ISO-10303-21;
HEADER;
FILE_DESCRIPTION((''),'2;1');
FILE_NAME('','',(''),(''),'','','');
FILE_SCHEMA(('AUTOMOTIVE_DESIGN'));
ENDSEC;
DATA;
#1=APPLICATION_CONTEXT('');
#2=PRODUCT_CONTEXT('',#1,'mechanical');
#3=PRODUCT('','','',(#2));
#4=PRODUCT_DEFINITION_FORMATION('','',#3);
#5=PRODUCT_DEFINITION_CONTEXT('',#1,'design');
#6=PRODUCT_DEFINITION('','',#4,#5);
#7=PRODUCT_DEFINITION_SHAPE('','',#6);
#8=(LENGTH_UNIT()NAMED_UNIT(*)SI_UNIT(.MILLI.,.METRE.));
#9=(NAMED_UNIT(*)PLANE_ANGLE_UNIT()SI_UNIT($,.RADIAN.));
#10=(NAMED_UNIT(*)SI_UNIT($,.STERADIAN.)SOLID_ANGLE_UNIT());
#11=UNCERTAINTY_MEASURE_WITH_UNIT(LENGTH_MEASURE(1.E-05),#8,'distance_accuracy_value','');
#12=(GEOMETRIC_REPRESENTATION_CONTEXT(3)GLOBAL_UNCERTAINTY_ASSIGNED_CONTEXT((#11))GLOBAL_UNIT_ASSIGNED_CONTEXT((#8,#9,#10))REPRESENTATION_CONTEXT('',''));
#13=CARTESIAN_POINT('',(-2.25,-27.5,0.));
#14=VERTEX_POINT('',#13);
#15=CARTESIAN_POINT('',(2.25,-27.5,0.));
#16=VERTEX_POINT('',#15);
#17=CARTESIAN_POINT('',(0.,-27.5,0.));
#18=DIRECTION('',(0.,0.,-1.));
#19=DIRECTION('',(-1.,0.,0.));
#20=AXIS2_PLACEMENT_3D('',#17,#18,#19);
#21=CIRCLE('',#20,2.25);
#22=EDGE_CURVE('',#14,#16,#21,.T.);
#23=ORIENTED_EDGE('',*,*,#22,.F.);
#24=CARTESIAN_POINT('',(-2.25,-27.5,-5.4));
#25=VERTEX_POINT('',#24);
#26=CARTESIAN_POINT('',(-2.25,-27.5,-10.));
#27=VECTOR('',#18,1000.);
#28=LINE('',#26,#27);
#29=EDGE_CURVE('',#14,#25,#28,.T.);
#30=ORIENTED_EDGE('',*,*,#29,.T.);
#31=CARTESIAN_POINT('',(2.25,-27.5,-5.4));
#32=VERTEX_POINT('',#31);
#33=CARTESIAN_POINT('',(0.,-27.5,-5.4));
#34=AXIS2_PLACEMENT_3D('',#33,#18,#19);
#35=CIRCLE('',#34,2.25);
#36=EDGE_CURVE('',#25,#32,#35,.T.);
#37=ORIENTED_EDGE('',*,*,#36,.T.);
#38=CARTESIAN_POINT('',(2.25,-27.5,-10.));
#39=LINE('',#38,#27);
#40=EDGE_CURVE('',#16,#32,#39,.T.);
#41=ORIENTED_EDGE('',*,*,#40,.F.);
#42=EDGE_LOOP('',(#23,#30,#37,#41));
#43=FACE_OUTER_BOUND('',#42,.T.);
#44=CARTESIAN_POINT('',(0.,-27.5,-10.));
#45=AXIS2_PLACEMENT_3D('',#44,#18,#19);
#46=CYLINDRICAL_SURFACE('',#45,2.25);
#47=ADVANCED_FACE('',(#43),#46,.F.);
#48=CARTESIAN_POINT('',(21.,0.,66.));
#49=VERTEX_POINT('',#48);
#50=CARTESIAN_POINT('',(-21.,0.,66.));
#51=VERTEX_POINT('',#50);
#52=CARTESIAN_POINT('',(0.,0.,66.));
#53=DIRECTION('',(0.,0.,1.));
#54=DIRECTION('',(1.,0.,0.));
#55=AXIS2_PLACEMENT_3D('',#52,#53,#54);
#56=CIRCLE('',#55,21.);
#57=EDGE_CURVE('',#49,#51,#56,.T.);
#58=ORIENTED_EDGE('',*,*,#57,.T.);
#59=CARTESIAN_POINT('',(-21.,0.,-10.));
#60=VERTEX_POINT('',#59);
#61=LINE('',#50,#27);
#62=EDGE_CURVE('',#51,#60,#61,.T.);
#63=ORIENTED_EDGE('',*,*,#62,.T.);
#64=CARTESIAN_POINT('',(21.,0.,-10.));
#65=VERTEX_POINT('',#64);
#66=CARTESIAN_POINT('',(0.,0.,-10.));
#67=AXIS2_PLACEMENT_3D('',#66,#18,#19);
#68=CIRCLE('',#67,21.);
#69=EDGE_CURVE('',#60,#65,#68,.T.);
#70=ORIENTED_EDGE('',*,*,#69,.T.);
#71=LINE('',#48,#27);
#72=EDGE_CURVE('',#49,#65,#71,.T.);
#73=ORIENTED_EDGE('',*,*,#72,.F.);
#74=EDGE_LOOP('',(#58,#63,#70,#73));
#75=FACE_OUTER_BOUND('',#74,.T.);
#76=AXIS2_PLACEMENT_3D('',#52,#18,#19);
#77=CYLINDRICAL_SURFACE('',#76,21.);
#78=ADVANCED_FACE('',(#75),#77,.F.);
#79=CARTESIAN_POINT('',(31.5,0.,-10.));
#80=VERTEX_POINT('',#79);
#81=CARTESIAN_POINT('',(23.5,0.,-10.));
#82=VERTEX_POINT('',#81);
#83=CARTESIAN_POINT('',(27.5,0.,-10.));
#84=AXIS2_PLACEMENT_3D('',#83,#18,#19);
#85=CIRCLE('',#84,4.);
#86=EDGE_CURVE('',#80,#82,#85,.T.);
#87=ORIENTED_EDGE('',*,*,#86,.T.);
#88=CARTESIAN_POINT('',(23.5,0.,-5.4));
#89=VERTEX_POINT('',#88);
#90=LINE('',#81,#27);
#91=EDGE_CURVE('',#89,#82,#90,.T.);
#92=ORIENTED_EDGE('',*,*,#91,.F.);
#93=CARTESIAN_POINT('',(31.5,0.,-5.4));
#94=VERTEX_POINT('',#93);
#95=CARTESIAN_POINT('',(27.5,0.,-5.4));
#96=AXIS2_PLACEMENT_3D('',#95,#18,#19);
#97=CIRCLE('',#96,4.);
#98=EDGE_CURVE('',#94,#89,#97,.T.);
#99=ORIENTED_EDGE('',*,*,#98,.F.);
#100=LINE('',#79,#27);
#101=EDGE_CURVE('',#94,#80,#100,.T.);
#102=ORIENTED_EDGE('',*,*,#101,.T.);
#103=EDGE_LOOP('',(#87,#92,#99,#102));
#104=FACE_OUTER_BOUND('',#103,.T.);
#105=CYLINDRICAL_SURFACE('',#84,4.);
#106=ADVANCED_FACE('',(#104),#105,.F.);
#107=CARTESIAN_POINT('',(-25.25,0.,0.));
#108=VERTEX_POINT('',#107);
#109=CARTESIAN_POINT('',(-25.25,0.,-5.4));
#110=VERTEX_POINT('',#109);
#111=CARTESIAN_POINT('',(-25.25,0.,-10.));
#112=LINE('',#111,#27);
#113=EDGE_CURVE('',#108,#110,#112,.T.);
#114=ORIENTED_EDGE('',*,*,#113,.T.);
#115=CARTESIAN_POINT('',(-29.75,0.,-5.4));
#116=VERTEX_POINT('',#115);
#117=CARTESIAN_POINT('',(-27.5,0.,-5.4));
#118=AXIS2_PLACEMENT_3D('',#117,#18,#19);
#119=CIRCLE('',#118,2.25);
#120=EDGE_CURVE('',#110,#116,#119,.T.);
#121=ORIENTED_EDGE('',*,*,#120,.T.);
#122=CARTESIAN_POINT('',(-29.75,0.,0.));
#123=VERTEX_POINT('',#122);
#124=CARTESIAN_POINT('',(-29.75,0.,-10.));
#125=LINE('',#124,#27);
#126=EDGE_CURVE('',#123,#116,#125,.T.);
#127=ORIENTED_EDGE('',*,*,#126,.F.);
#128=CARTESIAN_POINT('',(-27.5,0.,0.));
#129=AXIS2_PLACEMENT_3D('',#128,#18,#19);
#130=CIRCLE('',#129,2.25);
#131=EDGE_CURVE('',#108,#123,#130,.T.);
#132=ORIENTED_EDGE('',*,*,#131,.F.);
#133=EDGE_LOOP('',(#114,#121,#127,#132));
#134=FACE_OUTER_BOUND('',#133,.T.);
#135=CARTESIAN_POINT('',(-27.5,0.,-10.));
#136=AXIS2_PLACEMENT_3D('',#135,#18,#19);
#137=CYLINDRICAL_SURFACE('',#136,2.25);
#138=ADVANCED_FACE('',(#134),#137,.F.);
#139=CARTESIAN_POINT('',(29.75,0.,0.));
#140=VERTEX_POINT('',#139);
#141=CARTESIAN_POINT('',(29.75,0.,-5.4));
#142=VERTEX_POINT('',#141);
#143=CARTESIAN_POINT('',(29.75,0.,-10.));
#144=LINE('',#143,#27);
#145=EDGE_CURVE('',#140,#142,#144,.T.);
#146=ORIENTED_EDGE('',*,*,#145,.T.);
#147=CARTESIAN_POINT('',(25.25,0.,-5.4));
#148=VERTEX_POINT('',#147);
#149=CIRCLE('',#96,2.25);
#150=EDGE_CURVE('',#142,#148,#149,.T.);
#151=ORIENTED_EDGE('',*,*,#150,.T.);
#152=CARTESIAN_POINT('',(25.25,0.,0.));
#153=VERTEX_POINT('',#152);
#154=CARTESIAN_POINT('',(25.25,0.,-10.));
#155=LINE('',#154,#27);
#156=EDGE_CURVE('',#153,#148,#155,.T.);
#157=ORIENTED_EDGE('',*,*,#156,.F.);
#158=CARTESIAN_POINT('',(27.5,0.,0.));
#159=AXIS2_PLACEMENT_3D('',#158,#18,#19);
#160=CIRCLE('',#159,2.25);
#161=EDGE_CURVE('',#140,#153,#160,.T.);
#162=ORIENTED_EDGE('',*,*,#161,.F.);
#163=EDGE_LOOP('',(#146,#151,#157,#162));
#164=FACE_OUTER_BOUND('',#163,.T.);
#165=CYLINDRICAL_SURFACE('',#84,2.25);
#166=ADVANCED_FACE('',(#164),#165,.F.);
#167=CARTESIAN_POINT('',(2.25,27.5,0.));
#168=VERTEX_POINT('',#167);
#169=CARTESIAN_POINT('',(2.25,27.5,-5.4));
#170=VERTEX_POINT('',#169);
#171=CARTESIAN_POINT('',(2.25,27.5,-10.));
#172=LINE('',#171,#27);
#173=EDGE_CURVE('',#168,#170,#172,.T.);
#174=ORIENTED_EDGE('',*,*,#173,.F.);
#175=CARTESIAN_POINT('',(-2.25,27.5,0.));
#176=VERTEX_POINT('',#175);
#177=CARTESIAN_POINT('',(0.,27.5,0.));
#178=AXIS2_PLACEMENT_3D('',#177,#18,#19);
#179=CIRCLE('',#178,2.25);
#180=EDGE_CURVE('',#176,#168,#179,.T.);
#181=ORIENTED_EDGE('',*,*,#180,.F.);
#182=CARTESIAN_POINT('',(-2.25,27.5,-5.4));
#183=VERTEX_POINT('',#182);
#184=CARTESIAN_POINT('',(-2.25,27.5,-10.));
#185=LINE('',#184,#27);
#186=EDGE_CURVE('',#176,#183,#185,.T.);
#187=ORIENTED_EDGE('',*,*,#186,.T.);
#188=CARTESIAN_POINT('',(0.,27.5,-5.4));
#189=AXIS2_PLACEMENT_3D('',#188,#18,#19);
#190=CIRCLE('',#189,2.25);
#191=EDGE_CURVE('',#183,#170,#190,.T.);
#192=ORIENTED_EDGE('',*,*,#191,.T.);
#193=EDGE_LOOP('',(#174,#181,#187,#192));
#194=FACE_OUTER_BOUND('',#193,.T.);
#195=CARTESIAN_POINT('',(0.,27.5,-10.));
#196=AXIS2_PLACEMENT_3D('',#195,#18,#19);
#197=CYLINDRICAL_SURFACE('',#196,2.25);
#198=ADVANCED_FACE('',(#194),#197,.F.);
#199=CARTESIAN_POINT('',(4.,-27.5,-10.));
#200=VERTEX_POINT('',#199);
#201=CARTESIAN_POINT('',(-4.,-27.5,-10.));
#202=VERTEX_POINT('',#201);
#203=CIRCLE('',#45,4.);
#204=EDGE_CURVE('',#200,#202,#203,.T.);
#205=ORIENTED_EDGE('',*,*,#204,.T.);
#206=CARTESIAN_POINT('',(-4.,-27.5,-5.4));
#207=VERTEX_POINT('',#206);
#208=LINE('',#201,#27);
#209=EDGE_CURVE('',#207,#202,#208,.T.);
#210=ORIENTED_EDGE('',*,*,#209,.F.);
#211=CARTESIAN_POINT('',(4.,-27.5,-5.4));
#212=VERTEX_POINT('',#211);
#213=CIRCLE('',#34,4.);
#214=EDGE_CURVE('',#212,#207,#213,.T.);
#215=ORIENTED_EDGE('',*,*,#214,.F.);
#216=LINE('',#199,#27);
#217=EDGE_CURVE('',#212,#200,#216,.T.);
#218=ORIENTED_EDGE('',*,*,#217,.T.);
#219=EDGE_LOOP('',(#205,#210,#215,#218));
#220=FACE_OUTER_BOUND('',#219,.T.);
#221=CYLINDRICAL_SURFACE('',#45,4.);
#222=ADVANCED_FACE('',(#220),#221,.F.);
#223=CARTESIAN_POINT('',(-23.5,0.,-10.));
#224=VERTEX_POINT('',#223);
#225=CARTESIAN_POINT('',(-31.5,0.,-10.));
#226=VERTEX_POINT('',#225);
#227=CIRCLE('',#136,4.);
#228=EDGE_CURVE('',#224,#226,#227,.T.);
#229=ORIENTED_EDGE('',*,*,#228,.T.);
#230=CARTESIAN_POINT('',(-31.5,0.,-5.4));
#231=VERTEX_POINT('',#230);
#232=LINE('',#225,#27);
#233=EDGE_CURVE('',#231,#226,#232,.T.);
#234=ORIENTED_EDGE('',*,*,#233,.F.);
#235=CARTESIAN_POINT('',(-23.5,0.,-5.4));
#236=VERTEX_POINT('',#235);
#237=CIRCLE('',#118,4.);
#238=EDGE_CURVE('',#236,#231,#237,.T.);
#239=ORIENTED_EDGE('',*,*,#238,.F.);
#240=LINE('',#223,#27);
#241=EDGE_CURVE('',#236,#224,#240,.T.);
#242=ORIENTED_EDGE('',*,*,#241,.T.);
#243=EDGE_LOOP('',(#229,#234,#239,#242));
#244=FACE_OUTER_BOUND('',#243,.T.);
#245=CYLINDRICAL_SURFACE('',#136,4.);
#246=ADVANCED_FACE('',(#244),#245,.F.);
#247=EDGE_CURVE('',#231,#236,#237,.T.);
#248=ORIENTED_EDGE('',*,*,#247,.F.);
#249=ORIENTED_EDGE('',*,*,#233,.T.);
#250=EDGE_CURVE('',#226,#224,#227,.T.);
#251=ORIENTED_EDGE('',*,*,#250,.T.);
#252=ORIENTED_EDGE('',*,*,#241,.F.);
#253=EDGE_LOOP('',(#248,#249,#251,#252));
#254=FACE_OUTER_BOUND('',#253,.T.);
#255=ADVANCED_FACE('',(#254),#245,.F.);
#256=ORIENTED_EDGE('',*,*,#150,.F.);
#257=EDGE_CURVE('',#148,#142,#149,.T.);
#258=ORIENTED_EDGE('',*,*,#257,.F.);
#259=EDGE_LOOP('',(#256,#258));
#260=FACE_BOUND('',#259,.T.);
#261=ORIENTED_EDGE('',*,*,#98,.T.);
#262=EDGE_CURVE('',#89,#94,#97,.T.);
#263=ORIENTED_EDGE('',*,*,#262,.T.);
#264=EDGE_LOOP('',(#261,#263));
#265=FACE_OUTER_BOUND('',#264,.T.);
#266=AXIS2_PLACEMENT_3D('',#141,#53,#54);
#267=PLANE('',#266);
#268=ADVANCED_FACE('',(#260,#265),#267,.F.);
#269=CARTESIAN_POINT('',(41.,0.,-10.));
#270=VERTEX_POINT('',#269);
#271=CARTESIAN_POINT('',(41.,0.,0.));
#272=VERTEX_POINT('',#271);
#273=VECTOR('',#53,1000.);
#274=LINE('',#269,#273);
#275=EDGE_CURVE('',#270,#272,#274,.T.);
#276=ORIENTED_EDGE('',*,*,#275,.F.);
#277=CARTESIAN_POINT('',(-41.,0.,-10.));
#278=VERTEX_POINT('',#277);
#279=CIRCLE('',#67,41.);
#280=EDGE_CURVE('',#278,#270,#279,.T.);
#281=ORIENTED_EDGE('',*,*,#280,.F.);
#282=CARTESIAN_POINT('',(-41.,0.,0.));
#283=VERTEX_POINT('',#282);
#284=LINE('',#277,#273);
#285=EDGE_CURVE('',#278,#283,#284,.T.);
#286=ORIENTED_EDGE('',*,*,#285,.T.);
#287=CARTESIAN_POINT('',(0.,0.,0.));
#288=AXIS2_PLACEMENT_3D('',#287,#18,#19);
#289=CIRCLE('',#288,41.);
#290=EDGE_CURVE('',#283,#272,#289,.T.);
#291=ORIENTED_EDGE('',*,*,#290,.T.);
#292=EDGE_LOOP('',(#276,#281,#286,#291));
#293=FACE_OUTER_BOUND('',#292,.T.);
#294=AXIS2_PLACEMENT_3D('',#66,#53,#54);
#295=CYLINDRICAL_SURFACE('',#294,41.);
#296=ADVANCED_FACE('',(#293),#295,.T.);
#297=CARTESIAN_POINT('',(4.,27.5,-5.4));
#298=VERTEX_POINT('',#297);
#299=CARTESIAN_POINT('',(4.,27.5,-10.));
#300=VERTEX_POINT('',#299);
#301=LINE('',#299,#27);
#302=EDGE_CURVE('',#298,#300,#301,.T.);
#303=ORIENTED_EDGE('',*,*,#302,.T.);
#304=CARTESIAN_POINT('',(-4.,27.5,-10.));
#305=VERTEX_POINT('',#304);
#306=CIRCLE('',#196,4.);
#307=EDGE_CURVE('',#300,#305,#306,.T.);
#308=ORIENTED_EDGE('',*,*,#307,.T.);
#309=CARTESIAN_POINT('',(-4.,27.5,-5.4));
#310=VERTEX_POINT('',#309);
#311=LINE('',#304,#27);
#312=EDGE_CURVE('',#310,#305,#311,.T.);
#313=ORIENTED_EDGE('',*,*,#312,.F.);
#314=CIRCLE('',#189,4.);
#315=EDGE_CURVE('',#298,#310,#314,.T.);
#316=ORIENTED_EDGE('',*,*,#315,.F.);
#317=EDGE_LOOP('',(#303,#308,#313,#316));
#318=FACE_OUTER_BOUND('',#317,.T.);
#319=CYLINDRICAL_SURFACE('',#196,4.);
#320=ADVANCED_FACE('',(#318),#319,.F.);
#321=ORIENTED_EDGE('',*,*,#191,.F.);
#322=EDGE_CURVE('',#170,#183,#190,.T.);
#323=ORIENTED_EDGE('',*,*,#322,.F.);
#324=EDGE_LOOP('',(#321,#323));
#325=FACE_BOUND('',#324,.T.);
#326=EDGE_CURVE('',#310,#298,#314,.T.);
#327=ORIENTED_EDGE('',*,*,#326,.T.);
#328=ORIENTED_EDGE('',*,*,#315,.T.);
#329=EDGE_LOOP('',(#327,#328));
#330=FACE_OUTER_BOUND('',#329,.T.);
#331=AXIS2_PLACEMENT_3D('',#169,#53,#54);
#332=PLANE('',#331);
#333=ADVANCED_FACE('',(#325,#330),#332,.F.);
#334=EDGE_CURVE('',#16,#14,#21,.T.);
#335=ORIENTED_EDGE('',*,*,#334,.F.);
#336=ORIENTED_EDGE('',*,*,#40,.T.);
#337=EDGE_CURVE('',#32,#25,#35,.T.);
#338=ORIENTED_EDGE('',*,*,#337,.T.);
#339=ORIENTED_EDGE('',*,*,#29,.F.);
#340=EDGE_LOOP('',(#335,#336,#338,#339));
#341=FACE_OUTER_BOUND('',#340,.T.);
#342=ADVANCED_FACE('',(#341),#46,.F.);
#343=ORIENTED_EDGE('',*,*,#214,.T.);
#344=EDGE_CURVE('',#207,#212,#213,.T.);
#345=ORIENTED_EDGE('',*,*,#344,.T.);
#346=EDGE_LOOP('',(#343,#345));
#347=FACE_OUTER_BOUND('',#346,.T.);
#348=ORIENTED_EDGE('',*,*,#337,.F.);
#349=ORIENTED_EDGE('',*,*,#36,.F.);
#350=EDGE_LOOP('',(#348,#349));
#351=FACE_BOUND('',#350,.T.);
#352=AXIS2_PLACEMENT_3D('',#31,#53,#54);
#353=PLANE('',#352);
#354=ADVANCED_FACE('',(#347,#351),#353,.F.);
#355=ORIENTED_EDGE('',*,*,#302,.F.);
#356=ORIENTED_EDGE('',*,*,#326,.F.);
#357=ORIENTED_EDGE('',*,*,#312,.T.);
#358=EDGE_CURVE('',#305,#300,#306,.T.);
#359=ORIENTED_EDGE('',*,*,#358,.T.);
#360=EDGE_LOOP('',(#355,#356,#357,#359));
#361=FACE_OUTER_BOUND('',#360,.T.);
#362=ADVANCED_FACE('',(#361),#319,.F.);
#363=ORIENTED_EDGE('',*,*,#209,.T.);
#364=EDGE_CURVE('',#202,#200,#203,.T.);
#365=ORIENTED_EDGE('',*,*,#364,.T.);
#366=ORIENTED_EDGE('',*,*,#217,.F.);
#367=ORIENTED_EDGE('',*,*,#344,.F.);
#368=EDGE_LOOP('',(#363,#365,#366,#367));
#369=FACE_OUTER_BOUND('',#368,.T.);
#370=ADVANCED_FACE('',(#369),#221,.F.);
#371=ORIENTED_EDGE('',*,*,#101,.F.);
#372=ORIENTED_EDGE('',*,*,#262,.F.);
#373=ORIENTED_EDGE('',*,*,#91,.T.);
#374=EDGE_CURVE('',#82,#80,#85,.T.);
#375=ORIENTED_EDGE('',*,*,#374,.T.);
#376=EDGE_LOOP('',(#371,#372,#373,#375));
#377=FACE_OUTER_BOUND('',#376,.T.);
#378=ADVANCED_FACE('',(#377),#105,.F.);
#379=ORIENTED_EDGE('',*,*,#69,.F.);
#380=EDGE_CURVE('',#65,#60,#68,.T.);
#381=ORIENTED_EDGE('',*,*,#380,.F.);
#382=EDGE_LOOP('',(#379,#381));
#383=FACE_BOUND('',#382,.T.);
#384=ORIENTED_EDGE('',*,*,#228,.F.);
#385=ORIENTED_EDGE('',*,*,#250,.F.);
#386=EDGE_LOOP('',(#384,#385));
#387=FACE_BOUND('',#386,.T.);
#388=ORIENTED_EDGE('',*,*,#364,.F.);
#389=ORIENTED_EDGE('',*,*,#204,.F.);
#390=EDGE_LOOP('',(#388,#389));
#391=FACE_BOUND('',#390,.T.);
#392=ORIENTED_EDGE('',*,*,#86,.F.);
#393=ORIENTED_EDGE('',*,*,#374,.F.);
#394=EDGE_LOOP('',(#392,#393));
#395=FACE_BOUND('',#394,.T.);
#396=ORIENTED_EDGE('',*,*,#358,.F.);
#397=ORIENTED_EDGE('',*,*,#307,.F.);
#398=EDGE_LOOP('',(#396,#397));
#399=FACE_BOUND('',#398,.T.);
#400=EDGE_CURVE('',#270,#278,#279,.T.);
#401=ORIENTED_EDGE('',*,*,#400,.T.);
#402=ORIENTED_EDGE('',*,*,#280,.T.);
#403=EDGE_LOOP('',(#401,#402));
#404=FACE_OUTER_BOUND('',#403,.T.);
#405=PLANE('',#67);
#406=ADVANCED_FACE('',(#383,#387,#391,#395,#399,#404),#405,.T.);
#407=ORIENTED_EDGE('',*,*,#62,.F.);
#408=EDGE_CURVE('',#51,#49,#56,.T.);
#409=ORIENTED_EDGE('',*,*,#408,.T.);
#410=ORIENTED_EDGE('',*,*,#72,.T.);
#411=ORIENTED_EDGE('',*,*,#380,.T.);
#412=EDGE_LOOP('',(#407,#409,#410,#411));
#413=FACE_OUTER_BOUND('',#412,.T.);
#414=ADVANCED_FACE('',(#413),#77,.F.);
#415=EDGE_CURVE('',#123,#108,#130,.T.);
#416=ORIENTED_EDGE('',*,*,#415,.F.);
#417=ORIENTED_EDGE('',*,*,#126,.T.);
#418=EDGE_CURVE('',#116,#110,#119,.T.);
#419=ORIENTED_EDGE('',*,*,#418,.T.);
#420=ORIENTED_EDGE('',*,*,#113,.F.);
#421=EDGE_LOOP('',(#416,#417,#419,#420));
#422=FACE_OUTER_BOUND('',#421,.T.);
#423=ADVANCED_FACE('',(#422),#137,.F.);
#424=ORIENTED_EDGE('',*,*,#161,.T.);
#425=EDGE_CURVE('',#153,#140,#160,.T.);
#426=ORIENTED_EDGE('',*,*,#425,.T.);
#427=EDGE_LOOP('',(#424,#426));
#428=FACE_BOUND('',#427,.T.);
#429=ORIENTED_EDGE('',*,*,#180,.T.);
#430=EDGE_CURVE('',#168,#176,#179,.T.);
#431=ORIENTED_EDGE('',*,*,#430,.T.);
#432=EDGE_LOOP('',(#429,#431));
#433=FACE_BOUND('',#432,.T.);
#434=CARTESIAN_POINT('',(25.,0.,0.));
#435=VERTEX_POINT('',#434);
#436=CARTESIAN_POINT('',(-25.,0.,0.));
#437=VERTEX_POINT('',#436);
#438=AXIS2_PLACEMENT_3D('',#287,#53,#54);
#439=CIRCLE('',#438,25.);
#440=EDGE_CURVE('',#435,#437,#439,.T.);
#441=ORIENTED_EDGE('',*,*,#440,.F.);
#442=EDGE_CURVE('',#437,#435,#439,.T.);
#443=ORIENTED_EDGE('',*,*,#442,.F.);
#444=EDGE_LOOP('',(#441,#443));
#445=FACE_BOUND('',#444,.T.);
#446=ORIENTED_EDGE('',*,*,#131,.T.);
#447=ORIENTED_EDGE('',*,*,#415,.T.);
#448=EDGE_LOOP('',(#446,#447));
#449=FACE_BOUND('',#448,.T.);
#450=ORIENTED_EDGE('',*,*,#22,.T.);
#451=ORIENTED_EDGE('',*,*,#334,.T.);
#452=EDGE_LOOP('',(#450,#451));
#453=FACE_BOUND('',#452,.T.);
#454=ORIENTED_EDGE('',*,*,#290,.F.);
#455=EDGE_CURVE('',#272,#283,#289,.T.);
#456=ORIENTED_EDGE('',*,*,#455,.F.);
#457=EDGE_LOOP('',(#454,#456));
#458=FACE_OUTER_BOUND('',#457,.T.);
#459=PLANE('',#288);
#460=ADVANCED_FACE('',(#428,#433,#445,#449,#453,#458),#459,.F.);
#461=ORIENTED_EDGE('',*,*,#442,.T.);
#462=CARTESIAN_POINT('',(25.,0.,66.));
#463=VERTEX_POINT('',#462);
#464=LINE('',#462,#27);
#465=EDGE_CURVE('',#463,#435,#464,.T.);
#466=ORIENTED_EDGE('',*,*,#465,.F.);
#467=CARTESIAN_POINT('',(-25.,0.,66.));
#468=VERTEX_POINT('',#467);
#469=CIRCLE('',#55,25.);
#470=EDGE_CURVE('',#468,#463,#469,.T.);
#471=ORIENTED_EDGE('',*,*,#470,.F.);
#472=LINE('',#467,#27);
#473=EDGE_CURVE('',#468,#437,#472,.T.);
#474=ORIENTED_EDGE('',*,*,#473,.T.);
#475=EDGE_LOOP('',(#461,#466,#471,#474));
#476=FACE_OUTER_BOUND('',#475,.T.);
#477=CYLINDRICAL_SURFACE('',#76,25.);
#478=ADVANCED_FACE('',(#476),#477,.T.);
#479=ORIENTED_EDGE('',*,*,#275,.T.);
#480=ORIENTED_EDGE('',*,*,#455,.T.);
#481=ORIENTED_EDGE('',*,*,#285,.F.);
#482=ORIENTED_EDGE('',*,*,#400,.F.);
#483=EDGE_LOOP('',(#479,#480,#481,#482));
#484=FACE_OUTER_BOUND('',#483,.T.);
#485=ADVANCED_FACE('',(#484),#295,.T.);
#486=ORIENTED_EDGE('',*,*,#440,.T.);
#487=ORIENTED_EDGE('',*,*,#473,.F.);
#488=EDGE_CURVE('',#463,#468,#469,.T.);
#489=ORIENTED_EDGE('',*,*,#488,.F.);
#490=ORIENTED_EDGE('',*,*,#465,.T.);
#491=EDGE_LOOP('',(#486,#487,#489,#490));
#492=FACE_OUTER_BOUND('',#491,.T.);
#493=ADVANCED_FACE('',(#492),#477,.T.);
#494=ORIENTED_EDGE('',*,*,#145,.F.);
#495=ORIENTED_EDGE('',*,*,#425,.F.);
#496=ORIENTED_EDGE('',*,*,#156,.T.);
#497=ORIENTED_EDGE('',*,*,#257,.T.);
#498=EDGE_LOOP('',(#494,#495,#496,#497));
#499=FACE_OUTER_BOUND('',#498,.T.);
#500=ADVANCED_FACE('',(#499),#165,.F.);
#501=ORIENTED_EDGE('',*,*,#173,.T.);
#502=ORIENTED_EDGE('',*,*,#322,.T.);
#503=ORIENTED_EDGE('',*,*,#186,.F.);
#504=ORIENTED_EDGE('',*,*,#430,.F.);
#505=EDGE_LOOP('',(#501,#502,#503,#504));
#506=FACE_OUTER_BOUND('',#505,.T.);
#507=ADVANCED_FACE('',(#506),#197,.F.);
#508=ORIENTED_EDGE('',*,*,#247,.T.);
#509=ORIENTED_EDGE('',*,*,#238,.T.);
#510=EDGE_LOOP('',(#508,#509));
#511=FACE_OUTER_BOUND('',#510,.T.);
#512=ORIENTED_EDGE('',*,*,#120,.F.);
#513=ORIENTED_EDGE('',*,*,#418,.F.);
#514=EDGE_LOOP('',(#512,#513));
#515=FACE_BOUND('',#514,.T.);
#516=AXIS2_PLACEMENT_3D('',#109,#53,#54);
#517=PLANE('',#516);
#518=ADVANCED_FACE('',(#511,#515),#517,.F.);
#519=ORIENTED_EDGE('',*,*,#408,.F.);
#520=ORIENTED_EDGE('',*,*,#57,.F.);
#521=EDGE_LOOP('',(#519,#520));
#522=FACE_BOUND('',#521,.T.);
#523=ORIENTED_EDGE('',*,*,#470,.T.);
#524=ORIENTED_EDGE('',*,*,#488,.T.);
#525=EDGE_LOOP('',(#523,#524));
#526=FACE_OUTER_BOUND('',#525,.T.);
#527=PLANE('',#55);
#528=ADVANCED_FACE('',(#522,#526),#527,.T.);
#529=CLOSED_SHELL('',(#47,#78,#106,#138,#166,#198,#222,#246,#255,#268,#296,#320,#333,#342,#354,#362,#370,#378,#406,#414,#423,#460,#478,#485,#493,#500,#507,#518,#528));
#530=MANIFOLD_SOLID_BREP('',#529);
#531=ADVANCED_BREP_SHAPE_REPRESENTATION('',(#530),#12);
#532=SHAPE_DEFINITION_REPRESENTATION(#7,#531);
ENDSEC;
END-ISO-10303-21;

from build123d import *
from build123d.topology import SkipClean

# Parameters (mm, degrees)
SKETCH_1_R                = 25
SKETCH_1_R_2              = 21
EXTRUDE_1_DEPTH           = 66
EXTRUDE_START             = 10
SKETCH_2_R                = 41
SKETCH_2_R_2              = 21
EXTRUDE_2_DEPTH           = 10
HOLE_WIZARD_1_D           = 4.5
HOLE_WIZARD_1_CBORE_D     = 8
HOLE_WIZARD_1_CBORE_DEPTH = 4.6
PATTERN_CIRCULAR_1_COUNT  = 4


with BuildPart() as part:
    # 草图1 → 凸台-拉伸1 (new body)
    with BuildSketch(Plane.XY):
        Circle(SKETCH_1_R)
        Circle(SKETCH_1_R_2, mode=Mode.SUBTRACT)
    extrude(amount=EXTRUDE_1_DEPTH)

    # 草图2 → 凸台-拉伸2 (add)
    with SkipClean():  # the faces are left unmerged after this step: merging them gives an invalid solid
        with BuildSketch(Plane(origin=(0, 0, 0), x_dir=(-1, 0, 0), z_dir=(0, 0, -1)).offset(EXTRUDE_START)):
            Circle(SKETCH_2_R)
            Circle(SKETCH_2_R_2, mode=Mode.SUBTRACT)
        extrude(amount=-EXTRUDE_2_DEPTH)

    # 打孔尺寸(%根据)内六角圆柱头螺钉的类型1 (through all)
    with Locations(Plane(origin=(0, -27.5, -10), x_dir=(-1, 0, 0), z_dir=(0, 0, -1))):
        with Locations((0, 0)):
            hole_wizard_1 = CounterBoreHole(HOLE_WIZARD_1_D / 2, HOLE_WIZARD_1_CBORE_D / 2, HOLE_WIZARD_1_CBORE_DEPTH)

    # 阵列(圆周)1: 打孔尺寸(%根据)内六角圆柱头螺钉的类型1 ×4 about axis
    with SkipClean():  # the faces are left unmerged after this step: merging them gives an invalid solid
        pattern_circular_1_axis = Axis((0, 0, 0), (0, 0, 1))
        for i in range(1, PATTERN_CIRCULAR_1_COUNT):
            add(hole_wizard_1.rotate(pattern_circular_1_axis, i * 360 / PATTERN_CIRCULAR_1_COUNT), mode=Mode.SUBTRACT)


solid = part.part
